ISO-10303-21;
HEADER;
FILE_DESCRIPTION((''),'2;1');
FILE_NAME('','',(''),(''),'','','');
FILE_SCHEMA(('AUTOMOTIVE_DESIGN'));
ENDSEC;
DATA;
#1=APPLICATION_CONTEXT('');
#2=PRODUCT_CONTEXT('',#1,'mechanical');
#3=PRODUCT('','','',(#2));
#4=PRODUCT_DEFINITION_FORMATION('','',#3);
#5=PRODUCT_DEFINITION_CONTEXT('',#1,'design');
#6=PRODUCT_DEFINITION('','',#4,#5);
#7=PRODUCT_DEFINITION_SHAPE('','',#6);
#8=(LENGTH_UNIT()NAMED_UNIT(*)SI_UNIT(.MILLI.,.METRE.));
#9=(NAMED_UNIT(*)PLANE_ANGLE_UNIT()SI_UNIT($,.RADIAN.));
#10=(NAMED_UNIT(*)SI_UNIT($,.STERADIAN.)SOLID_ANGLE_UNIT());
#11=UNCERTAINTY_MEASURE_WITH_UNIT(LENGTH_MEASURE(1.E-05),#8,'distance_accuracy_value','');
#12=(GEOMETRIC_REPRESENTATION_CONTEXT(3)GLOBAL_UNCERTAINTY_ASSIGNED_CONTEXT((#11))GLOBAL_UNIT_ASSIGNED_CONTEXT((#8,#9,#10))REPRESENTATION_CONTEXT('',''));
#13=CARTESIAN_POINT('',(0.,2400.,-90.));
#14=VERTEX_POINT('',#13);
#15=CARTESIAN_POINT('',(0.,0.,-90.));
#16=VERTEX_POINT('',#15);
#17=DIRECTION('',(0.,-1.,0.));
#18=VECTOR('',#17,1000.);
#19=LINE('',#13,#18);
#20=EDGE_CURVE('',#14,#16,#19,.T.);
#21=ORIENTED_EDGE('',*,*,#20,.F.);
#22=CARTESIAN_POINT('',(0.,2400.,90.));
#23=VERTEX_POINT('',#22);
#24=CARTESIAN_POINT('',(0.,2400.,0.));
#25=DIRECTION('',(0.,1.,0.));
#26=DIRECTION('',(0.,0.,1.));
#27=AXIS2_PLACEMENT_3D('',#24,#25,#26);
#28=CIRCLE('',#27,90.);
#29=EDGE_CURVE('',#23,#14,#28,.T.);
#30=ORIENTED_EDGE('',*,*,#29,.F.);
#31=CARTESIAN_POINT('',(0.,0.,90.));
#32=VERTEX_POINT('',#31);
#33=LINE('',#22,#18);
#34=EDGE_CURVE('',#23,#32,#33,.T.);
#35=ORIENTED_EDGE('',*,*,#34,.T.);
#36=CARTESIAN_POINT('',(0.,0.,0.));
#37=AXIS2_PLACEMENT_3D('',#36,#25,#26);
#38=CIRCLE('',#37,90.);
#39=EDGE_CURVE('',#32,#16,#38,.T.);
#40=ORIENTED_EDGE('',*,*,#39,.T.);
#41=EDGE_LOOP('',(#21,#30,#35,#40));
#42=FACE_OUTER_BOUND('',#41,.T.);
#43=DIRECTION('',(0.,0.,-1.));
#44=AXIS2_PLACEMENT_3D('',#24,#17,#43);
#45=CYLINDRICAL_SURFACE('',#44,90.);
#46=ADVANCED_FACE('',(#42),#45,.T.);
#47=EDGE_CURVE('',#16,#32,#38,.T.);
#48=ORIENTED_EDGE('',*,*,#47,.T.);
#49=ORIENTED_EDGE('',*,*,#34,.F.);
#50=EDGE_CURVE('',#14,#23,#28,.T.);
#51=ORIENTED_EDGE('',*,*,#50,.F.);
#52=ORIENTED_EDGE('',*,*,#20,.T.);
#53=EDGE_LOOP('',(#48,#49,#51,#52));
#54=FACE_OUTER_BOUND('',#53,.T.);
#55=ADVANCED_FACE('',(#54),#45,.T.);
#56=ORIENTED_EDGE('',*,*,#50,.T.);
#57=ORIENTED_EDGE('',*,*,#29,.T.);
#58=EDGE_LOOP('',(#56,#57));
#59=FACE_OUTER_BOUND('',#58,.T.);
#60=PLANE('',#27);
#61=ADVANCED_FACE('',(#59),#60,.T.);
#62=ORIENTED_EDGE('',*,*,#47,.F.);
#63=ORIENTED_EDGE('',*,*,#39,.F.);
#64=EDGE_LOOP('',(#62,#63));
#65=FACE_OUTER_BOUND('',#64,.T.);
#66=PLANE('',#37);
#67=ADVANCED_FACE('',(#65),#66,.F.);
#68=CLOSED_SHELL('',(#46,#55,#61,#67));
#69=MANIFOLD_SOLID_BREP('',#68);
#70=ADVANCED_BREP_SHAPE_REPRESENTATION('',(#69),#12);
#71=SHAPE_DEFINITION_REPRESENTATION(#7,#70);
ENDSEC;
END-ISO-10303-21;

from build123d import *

# Parameters (mm, degrees)
SKETCH1_R           = 90
BOSS_EXTRUDE1_DEPTH = 2400


with BuildPart() as part:
    # Sketch1 → Boss-Extrude1 (new body)
    with BuildSketch(Plane(origin=(0, 0, 0), x_dir=(1, 0, 0), z_dir=(0, 1, 0))):
        with Locations(Location((0, 0, 0), (0, 0, 270))):
            Circle(SKETCH1_R)
    extrude(amount=BOSS_EXTRUDE1_DEPTH)


solid = part.part
